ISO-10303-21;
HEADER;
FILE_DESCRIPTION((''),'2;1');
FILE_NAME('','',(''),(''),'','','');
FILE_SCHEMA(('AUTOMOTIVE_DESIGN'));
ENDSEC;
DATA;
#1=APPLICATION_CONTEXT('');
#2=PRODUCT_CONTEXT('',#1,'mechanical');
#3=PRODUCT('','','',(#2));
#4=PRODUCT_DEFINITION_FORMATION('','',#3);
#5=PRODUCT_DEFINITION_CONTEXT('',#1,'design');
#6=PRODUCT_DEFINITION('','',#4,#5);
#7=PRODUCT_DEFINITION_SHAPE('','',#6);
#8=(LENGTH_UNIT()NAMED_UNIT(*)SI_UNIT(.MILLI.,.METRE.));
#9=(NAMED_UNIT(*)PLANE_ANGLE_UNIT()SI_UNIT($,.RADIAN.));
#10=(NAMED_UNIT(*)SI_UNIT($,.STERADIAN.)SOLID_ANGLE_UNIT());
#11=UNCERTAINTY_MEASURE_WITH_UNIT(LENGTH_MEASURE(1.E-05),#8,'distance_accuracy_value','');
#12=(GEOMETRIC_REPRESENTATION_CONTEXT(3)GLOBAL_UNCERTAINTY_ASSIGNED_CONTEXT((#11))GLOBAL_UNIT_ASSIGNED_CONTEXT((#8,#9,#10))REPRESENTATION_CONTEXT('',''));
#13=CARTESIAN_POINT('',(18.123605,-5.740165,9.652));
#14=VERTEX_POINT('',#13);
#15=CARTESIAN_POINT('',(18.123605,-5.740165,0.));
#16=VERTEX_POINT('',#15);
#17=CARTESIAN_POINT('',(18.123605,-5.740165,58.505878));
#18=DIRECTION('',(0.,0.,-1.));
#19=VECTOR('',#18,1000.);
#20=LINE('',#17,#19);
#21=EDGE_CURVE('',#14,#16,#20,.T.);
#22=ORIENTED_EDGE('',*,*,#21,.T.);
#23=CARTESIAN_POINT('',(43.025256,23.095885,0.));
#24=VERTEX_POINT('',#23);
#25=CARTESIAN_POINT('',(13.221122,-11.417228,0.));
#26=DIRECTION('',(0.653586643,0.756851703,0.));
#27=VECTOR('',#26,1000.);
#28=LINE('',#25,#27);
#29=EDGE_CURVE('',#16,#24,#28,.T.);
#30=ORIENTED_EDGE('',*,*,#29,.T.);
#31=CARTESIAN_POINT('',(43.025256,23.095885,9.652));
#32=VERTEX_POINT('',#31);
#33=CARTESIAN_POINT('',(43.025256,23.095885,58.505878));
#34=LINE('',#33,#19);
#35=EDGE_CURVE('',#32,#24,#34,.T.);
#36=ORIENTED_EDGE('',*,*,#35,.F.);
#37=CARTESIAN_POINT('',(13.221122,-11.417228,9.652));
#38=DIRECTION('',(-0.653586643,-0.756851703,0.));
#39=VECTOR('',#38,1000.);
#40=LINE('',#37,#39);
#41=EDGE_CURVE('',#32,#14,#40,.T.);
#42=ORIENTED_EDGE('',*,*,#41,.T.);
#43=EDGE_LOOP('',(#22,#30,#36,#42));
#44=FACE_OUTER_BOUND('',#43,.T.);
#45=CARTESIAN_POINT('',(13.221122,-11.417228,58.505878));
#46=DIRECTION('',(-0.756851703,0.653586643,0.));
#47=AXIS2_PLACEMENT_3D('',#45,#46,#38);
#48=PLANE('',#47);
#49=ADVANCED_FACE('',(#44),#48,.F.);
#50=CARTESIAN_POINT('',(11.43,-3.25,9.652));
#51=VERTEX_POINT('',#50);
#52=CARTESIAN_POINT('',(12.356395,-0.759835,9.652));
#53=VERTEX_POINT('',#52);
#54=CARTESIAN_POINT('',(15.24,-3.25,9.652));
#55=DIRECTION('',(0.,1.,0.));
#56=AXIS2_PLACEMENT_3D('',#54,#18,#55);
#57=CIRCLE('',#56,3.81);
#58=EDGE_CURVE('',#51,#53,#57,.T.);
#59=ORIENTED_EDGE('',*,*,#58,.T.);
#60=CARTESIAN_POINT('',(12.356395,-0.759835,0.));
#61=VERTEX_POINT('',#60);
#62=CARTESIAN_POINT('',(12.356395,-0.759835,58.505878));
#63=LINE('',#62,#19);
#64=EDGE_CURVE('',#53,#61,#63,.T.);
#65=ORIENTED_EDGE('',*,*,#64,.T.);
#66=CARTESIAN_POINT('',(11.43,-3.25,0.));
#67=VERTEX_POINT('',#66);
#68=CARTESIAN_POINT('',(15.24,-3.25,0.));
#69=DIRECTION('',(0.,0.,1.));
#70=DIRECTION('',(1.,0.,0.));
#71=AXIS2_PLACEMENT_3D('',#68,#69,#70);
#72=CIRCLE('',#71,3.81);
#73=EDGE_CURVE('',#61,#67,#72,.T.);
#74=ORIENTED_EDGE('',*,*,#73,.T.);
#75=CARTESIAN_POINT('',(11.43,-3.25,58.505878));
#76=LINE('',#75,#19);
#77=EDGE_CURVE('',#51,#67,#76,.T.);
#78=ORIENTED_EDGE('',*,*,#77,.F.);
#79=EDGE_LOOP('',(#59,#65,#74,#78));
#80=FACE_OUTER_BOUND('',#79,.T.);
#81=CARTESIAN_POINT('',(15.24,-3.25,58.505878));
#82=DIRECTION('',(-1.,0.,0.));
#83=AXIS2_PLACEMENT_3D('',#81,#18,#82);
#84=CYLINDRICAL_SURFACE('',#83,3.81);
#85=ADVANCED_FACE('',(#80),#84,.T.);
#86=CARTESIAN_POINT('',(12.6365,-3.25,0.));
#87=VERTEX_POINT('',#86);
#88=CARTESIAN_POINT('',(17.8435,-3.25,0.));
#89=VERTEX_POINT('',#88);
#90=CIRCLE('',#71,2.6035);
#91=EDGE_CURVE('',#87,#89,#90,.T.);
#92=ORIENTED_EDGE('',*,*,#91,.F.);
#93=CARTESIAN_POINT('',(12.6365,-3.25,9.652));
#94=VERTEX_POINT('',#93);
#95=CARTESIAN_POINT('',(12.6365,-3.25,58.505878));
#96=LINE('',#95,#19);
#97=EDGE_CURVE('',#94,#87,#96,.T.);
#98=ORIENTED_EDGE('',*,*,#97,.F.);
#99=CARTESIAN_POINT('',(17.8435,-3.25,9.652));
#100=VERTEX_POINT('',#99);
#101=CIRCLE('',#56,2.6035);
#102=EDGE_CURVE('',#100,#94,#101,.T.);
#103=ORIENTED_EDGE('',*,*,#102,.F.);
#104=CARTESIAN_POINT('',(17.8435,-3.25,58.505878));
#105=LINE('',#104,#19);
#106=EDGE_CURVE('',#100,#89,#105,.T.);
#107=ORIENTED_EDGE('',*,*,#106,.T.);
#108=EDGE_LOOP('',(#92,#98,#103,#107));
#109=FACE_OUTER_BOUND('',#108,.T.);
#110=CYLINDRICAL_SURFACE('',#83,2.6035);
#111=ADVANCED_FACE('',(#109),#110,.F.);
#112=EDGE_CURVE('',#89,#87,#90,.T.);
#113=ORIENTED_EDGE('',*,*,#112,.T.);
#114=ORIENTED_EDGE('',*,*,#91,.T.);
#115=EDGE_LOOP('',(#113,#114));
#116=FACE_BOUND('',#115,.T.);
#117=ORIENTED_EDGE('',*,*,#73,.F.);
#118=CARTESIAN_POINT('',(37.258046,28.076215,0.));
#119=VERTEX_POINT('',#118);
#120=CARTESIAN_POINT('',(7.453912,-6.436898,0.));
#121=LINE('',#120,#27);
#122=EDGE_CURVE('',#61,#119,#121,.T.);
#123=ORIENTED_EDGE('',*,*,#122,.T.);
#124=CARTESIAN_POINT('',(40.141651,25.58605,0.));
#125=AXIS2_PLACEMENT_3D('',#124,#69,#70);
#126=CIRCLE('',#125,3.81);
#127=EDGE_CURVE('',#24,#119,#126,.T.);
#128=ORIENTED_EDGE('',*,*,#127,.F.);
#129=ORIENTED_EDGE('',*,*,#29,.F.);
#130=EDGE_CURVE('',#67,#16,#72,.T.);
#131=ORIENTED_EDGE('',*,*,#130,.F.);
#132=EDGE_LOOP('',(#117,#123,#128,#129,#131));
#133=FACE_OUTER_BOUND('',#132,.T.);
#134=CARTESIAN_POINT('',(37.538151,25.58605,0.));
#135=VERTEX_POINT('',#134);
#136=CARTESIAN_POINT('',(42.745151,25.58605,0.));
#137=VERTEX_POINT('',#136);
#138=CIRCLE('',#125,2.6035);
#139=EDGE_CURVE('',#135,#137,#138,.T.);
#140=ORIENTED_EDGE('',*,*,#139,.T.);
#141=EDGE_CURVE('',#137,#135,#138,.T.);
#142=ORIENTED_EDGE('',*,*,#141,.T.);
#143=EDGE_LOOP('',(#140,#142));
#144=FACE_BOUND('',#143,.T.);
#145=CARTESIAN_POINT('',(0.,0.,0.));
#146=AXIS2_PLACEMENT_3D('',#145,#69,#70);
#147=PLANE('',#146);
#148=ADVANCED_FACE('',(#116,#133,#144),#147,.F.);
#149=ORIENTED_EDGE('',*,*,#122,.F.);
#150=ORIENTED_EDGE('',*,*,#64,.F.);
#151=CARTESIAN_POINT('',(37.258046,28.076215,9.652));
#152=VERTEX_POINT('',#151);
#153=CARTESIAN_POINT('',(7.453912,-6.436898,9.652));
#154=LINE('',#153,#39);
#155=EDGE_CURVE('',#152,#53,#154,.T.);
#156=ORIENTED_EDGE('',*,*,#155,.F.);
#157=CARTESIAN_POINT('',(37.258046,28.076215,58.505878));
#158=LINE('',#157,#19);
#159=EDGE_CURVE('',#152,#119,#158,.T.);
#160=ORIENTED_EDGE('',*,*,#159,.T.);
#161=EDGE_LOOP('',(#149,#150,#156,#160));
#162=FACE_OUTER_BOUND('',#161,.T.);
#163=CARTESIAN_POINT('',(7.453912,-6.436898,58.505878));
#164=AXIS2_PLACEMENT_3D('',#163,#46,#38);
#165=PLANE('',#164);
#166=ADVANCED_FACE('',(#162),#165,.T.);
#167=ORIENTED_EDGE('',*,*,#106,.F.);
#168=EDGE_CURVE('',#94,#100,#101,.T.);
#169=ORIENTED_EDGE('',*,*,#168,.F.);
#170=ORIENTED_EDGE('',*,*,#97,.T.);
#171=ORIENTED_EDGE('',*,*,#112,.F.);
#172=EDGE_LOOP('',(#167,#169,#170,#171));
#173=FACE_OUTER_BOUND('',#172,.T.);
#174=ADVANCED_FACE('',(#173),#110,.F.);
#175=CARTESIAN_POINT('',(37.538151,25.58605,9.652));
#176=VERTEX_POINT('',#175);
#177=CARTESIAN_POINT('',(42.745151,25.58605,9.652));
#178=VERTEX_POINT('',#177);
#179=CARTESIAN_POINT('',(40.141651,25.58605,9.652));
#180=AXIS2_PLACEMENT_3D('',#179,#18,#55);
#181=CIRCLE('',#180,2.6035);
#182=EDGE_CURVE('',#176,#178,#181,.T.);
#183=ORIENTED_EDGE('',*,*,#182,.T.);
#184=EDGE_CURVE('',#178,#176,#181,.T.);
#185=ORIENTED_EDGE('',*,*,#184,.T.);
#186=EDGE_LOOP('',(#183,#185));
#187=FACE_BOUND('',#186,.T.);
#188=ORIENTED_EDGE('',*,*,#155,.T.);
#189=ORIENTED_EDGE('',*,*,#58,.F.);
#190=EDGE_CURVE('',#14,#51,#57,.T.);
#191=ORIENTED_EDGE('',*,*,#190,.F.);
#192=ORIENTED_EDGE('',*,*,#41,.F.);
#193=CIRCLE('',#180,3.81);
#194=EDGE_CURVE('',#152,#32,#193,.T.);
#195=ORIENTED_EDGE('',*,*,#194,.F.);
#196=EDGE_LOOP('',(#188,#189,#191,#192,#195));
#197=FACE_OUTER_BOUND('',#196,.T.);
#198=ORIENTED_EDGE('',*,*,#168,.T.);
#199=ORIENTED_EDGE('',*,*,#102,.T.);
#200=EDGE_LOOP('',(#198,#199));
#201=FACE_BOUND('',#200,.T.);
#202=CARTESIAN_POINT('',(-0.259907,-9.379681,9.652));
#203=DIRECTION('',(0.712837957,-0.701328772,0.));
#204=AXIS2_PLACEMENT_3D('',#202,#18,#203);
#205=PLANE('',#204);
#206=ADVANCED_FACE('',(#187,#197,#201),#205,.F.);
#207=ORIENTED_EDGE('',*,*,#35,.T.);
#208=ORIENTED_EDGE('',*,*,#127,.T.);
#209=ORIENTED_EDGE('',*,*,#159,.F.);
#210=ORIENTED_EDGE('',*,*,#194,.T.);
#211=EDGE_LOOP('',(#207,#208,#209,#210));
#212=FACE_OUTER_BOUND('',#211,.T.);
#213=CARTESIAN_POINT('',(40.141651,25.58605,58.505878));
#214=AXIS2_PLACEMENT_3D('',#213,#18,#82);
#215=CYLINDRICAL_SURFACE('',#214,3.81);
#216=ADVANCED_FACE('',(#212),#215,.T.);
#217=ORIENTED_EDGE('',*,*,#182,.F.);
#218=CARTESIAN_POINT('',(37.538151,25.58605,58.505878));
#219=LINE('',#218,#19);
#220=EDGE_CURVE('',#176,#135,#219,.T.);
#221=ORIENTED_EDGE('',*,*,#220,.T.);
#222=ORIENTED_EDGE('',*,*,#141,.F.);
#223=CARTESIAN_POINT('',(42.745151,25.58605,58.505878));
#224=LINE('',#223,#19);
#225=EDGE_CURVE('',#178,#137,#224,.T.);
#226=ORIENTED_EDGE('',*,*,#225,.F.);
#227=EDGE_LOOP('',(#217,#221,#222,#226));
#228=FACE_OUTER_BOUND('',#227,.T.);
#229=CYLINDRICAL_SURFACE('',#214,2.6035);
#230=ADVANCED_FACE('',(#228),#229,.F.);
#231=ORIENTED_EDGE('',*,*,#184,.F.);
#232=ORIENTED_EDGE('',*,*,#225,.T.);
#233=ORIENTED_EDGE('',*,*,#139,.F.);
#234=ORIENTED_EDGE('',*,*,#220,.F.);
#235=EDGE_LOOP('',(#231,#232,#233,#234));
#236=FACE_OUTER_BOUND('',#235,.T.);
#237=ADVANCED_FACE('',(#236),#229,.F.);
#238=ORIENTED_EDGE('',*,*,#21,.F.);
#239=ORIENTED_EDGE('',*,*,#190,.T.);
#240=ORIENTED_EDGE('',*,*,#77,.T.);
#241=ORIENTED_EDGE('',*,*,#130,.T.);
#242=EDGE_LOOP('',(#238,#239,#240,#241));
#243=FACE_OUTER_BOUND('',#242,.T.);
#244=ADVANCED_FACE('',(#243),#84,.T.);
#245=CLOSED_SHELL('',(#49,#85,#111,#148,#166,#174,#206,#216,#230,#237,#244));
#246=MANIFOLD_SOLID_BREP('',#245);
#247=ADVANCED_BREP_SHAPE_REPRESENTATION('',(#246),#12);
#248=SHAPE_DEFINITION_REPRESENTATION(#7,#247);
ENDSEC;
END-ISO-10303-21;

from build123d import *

# Parameters (mm, degrees)
SKETCH1_R           = 2.6035
BOSS_EXTRUDE1_DEPTH = 9.652


with BuildPart() as part:
    # Sketch1 → Boss-Extrude1 (new body)
    with BuildSketch(Plane.XY):
        with BuildLine():
            Line((12.356395011, -0.759834892), (37.258046093, 28.076215001))
            ThreePointArc((37.258046093, 28.076215001), (42.63181619, 28.469654882), (43.025256071, 23.095884784))
            Line((43.025256071, 23.095884784), (18.123604989, -5.740165108))
            ThreePointArc((18.123604989, -5.740165108), (12.749834892, -6.133604989), (12.356395011, -0.759834892))
        make_face()
        with Locations(Location((15.24, -3.25, 0), (0, 0, 90))):
            Circle(SKETCH1_R, mode=Mode.SUBTRACT)
        with Locations(Location((40.141651082, 25.586049892, 0), (0, 0, 90))):
            Circle(SKETCH1_R, mode=Mode.SUBTRACT)
    extrude(amount=BOSS_EXTRUDE1_DEPTH)


solid = part.part
